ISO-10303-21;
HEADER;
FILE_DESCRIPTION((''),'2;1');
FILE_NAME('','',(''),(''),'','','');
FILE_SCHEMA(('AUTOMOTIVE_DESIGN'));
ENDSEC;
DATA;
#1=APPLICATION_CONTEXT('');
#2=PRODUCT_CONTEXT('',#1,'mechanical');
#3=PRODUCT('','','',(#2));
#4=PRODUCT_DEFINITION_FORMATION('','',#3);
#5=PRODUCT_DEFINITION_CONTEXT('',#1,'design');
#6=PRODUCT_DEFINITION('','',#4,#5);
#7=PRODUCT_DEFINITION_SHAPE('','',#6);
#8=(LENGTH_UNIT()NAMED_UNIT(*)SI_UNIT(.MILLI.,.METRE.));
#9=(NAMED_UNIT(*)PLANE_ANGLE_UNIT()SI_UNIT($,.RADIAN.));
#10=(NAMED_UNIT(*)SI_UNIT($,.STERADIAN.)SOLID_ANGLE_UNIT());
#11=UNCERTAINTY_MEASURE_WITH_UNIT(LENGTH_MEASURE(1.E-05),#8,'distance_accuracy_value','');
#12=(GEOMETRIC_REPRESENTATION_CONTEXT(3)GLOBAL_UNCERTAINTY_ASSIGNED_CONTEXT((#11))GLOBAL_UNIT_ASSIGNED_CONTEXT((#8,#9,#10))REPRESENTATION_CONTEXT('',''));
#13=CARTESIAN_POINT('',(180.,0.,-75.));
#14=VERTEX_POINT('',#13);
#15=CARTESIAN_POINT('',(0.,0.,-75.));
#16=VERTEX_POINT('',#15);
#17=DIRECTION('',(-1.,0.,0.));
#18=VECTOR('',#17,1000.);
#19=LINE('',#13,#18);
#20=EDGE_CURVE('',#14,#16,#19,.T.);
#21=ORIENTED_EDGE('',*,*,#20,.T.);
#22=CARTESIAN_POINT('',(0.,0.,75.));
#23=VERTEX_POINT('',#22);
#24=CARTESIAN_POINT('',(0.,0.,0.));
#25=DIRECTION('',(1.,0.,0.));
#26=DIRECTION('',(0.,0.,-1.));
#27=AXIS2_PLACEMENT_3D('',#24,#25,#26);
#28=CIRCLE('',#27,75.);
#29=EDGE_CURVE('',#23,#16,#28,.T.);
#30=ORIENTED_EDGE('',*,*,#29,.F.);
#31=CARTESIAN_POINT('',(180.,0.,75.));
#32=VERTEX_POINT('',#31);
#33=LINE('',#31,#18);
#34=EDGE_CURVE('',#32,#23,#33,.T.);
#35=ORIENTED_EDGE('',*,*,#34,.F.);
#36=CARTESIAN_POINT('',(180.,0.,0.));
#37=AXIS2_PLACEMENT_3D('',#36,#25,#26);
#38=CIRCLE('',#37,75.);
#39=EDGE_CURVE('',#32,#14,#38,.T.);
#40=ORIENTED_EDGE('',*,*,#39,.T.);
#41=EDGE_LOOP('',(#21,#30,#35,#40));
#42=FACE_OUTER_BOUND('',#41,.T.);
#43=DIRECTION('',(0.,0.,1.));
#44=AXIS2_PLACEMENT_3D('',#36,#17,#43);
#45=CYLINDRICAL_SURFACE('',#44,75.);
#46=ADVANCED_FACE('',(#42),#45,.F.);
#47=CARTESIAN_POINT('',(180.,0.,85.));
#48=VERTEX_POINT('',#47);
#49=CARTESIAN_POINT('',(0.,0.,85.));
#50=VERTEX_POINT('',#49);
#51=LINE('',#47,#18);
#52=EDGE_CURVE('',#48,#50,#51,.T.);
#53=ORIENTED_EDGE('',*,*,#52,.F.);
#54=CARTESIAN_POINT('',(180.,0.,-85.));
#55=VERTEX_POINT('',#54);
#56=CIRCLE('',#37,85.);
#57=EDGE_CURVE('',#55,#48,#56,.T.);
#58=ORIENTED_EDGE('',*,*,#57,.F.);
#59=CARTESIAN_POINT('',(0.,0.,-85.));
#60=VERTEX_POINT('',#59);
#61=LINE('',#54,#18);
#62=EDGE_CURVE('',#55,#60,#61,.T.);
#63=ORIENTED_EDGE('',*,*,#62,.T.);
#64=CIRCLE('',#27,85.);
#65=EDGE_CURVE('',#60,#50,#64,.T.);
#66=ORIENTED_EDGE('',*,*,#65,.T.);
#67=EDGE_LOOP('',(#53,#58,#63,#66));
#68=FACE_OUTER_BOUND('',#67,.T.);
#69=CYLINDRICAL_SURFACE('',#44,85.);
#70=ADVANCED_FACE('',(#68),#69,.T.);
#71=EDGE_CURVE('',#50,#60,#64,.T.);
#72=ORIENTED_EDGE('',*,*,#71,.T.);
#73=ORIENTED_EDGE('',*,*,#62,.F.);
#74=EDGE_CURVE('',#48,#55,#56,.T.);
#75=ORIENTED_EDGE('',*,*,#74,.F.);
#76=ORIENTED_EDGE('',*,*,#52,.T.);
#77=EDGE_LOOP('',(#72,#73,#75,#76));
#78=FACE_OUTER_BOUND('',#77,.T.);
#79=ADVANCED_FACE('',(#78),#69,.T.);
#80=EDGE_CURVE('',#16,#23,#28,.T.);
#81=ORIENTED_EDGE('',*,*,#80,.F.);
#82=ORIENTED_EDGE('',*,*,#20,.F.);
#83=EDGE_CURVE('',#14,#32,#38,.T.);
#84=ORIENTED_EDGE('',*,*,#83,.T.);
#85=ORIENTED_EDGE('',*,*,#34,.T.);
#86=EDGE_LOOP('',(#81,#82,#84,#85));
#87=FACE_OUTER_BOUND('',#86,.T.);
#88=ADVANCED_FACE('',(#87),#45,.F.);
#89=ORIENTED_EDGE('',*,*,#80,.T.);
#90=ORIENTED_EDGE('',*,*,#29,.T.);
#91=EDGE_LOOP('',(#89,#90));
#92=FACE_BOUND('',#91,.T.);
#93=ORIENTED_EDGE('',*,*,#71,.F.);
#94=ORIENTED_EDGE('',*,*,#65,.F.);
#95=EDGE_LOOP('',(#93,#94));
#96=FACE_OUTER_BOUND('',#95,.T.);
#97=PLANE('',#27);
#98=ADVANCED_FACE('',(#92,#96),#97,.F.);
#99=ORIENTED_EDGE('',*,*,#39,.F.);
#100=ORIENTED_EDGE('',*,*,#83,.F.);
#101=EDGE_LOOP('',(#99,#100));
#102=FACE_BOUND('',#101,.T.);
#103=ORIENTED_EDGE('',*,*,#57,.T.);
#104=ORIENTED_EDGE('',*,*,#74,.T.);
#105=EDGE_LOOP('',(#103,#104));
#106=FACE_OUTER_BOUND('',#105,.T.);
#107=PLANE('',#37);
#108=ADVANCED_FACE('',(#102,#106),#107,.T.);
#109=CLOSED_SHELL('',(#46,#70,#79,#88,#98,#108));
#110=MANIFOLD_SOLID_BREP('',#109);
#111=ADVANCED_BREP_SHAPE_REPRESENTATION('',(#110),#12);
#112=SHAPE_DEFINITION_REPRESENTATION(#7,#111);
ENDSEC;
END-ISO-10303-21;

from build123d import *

# Parameters (mm, degrees)
SKETCH1_R           = 85
SKETCH1_R_2         = 75
BOSS_EXTRUDE1_DEPTH = 180


with BuildPart() as part:
    # Sketch1 → Boss-Extrude1 (new body)
    with BuildSketch(Plane(origin=(0, 0, 0), x_dir=(0, 0, -1), z_dir=(1, 0, 0))):
        with Locations(Location((0, 0, 0), (0, 0, 180))):
            Circle(SKETCH1_R)
        with Locations(Location((0, 0, 0), (0, 0, 180))):
            Circle(SKETCH1_R_2, mode=Mode.SUBTRACT)
    extrude(amount=BOSS_EXTRUDE1_DEPTH)


solid = part.part
